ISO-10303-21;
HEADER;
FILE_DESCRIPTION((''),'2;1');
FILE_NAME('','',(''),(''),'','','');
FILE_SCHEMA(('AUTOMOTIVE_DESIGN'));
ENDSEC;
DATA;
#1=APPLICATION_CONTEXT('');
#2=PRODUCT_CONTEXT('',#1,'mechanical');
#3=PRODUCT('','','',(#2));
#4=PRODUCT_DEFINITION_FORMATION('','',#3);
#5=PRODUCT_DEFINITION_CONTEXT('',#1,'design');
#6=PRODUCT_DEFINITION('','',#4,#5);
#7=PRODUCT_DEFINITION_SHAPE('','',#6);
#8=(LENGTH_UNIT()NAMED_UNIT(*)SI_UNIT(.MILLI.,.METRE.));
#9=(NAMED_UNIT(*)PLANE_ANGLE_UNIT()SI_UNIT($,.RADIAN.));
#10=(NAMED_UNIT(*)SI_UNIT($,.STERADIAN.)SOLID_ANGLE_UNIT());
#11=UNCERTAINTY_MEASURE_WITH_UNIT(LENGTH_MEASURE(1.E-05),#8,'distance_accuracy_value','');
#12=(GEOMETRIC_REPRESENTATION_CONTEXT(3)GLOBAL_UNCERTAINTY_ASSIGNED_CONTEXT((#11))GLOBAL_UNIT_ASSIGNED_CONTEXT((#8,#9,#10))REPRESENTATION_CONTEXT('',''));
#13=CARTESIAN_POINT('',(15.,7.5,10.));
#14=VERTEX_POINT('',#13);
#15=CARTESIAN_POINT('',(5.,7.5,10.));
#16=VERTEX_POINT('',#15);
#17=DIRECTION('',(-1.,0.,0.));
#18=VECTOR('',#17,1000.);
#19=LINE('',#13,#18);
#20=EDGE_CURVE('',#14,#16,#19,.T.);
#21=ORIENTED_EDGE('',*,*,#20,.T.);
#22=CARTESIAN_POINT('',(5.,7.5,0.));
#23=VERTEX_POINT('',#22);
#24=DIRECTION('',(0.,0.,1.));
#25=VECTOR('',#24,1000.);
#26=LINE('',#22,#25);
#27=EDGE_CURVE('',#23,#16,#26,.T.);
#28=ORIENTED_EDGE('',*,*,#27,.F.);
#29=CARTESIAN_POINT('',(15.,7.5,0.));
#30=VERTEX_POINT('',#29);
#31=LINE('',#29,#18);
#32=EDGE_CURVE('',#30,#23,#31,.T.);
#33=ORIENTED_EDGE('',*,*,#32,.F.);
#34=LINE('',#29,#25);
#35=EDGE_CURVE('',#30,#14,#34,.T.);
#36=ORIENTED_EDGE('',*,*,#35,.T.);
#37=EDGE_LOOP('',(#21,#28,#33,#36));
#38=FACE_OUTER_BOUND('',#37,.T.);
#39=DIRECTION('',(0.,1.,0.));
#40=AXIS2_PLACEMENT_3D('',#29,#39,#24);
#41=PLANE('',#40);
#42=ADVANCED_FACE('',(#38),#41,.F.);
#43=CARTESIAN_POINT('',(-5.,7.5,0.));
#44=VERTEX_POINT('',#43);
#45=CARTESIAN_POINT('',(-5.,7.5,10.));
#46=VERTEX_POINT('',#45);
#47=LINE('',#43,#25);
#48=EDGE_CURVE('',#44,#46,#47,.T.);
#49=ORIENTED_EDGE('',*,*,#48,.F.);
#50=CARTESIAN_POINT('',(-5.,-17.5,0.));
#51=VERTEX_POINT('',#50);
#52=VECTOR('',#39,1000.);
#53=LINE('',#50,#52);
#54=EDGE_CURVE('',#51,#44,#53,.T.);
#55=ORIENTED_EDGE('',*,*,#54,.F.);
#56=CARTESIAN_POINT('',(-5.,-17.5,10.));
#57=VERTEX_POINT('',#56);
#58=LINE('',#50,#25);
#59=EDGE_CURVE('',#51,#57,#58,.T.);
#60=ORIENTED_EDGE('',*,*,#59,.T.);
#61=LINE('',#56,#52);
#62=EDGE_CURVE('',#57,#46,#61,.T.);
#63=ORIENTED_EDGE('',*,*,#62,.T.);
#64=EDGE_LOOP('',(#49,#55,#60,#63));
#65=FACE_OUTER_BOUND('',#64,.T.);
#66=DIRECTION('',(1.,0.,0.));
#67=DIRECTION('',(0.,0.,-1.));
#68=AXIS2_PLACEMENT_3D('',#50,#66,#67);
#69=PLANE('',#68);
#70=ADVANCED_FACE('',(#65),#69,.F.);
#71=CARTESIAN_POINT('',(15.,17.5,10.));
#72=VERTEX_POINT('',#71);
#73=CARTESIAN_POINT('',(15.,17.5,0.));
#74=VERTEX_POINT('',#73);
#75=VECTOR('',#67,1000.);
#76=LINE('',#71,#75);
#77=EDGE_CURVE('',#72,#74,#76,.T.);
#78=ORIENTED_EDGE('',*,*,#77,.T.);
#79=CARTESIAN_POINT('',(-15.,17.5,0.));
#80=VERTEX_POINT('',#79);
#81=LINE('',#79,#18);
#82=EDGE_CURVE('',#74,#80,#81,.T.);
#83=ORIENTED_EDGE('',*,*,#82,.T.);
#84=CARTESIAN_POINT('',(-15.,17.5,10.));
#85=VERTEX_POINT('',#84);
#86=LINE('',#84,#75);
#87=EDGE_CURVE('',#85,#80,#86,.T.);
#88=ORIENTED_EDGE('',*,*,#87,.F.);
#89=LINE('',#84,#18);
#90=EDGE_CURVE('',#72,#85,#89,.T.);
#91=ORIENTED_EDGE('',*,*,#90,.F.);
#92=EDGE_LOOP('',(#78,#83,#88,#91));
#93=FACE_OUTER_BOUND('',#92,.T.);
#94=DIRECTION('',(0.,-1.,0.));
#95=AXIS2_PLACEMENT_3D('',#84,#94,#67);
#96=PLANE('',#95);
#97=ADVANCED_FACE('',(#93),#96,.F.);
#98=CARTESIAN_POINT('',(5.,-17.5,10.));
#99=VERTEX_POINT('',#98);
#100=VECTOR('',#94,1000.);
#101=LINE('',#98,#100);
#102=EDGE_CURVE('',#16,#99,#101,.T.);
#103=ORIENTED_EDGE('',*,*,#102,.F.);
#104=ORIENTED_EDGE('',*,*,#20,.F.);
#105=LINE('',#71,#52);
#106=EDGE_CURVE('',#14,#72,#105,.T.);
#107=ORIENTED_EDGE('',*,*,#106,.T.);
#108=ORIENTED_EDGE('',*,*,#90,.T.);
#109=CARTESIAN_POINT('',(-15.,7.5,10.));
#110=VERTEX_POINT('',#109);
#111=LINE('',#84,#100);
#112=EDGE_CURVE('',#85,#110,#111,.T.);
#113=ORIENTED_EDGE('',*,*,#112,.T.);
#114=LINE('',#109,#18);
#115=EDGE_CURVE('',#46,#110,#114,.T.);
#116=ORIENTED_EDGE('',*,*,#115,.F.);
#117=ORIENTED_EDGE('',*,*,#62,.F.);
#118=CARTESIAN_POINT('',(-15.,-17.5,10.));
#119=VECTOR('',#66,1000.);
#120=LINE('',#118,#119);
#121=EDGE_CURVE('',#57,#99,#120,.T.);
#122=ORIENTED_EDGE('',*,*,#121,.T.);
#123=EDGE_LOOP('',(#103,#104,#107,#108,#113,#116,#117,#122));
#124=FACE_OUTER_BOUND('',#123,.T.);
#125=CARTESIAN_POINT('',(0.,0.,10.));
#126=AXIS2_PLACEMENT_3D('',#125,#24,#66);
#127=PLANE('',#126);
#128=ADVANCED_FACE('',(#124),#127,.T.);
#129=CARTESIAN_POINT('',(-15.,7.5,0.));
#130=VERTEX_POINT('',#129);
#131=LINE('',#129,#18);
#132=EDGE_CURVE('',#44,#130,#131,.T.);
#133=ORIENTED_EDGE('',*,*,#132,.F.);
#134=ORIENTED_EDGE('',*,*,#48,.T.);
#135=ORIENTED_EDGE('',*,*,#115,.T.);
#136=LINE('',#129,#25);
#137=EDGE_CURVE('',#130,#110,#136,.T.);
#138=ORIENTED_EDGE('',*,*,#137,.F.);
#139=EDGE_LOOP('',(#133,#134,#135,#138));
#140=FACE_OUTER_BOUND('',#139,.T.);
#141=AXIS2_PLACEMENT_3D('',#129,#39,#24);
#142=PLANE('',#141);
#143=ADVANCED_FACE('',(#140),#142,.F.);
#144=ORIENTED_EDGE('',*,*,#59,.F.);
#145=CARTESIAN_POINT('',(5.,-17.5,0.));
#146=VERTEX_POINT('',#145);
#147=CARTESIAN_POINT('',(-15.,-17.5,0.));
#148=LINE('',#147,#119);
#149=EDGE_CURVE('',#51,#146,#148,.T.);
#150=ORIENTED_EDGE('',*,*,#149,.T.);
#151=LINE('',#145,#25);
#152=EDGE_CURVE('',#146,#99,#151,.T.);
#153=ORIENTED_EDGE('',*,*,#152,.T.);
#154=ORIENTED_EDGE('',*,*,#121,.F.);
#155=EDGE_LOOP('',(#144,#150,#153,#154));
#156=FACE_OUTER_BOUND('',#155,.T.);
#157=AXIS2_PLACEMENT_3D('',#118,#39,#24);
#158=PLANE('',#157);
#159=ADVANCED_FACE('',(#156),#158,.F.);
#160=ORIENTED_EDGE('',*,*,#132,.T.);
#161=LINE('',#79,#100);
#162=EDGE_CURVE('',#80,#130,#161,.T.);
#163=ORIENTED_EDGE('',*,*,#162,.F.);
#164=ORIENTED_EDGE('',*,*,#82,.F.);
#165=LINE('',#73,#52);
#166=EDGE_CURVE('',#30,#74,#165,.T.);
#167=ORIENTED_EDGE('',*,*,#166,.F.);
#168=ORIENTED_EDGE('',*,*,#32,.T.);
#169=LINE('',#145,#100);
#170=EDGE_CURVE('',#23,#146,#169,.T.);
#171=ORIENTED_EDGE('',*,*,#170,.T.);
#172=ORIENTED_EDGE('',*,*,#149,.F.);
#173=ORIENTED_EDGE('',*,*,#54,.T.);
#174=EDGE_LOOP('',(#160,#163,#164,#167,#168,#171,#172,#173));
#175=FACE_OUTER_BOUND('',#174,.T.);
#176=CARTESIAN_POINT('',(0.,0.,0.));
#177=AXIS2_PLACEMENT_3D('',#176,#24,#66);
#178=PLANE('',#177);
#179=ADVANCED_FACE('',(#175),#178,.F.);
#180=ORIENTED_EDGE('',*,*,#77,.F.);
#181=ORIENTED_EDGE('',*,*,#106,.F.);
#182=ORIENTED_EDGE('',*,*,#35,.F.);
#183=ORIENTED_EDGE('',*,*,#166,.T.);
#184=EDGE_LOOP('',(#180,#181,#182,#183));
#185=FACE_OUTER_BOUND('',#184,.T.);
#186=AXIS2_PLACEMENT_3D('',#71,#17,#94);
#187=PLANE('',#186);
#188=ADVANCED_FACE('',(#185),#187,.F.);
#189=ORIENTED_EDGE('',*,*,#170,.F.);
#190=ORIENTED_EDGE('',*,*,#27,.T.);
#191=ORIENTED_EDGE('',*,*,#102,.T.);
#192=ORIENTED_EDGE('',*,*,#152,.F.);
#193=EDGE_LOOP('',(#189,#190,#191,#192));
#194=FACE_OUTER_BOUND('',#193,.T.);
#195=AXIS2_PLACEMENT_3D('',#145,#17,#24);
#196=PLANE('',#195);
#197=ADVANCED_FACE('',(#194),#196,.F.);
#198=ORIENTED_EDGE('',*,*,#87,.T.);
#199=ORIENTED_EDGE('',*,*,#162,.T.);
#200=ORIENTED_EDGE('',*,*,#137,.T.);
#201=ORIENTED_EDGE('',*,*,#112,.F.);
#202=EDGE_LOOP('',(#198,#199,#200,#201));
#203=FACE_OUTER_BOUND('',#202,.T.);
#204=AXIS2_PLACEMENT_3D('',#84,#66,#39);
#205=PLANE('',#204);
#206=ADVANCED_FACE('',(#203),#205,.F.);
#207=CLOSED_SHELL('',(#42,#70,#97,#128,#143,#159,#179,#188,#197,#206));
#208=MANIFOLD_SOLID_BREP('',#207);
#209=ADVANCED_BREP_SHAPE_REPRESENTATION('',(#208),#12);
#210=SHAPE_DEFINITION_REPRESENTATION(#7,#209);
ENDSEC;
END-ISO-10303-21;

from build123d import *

# Parameters (mm, degrees)
SKETCH1_W           = 30
SKETCH1_H           = 35
BOSS_EXTRUDE1_DEPTH = 10
SKETCH2_W           = 10
SKETCH2_H           = 25
CUT_EXTRUDE1_DEPTH  = 26.124689053


with BuildPart() as part:
    # Sketch1 → Boss-Extrude1 (new body)
    with BuildSketch(Plane.XY):
        Rectangle(SKETCH1_W, SKETCH1_H)
    extrude(amount=BOSS_EXTRUDE1_DEPTH)

    # Sketch2 → Cut-Extrude1 (cut, through all)
    with BuildSketch(Plane.XY.offset(10)):
        with Locations((-10, -5)):
            Rectangle(SKETCH2_W, SKETCH2_H)
        with Locations((10, -5)):
            Rectangle(SKETCH2_W, SKETCH2_H)
    extrude(amount=-CUT_EXTRUDE1_DEPTH, mode=Mode.SUBTRACT)


solid = part.part
